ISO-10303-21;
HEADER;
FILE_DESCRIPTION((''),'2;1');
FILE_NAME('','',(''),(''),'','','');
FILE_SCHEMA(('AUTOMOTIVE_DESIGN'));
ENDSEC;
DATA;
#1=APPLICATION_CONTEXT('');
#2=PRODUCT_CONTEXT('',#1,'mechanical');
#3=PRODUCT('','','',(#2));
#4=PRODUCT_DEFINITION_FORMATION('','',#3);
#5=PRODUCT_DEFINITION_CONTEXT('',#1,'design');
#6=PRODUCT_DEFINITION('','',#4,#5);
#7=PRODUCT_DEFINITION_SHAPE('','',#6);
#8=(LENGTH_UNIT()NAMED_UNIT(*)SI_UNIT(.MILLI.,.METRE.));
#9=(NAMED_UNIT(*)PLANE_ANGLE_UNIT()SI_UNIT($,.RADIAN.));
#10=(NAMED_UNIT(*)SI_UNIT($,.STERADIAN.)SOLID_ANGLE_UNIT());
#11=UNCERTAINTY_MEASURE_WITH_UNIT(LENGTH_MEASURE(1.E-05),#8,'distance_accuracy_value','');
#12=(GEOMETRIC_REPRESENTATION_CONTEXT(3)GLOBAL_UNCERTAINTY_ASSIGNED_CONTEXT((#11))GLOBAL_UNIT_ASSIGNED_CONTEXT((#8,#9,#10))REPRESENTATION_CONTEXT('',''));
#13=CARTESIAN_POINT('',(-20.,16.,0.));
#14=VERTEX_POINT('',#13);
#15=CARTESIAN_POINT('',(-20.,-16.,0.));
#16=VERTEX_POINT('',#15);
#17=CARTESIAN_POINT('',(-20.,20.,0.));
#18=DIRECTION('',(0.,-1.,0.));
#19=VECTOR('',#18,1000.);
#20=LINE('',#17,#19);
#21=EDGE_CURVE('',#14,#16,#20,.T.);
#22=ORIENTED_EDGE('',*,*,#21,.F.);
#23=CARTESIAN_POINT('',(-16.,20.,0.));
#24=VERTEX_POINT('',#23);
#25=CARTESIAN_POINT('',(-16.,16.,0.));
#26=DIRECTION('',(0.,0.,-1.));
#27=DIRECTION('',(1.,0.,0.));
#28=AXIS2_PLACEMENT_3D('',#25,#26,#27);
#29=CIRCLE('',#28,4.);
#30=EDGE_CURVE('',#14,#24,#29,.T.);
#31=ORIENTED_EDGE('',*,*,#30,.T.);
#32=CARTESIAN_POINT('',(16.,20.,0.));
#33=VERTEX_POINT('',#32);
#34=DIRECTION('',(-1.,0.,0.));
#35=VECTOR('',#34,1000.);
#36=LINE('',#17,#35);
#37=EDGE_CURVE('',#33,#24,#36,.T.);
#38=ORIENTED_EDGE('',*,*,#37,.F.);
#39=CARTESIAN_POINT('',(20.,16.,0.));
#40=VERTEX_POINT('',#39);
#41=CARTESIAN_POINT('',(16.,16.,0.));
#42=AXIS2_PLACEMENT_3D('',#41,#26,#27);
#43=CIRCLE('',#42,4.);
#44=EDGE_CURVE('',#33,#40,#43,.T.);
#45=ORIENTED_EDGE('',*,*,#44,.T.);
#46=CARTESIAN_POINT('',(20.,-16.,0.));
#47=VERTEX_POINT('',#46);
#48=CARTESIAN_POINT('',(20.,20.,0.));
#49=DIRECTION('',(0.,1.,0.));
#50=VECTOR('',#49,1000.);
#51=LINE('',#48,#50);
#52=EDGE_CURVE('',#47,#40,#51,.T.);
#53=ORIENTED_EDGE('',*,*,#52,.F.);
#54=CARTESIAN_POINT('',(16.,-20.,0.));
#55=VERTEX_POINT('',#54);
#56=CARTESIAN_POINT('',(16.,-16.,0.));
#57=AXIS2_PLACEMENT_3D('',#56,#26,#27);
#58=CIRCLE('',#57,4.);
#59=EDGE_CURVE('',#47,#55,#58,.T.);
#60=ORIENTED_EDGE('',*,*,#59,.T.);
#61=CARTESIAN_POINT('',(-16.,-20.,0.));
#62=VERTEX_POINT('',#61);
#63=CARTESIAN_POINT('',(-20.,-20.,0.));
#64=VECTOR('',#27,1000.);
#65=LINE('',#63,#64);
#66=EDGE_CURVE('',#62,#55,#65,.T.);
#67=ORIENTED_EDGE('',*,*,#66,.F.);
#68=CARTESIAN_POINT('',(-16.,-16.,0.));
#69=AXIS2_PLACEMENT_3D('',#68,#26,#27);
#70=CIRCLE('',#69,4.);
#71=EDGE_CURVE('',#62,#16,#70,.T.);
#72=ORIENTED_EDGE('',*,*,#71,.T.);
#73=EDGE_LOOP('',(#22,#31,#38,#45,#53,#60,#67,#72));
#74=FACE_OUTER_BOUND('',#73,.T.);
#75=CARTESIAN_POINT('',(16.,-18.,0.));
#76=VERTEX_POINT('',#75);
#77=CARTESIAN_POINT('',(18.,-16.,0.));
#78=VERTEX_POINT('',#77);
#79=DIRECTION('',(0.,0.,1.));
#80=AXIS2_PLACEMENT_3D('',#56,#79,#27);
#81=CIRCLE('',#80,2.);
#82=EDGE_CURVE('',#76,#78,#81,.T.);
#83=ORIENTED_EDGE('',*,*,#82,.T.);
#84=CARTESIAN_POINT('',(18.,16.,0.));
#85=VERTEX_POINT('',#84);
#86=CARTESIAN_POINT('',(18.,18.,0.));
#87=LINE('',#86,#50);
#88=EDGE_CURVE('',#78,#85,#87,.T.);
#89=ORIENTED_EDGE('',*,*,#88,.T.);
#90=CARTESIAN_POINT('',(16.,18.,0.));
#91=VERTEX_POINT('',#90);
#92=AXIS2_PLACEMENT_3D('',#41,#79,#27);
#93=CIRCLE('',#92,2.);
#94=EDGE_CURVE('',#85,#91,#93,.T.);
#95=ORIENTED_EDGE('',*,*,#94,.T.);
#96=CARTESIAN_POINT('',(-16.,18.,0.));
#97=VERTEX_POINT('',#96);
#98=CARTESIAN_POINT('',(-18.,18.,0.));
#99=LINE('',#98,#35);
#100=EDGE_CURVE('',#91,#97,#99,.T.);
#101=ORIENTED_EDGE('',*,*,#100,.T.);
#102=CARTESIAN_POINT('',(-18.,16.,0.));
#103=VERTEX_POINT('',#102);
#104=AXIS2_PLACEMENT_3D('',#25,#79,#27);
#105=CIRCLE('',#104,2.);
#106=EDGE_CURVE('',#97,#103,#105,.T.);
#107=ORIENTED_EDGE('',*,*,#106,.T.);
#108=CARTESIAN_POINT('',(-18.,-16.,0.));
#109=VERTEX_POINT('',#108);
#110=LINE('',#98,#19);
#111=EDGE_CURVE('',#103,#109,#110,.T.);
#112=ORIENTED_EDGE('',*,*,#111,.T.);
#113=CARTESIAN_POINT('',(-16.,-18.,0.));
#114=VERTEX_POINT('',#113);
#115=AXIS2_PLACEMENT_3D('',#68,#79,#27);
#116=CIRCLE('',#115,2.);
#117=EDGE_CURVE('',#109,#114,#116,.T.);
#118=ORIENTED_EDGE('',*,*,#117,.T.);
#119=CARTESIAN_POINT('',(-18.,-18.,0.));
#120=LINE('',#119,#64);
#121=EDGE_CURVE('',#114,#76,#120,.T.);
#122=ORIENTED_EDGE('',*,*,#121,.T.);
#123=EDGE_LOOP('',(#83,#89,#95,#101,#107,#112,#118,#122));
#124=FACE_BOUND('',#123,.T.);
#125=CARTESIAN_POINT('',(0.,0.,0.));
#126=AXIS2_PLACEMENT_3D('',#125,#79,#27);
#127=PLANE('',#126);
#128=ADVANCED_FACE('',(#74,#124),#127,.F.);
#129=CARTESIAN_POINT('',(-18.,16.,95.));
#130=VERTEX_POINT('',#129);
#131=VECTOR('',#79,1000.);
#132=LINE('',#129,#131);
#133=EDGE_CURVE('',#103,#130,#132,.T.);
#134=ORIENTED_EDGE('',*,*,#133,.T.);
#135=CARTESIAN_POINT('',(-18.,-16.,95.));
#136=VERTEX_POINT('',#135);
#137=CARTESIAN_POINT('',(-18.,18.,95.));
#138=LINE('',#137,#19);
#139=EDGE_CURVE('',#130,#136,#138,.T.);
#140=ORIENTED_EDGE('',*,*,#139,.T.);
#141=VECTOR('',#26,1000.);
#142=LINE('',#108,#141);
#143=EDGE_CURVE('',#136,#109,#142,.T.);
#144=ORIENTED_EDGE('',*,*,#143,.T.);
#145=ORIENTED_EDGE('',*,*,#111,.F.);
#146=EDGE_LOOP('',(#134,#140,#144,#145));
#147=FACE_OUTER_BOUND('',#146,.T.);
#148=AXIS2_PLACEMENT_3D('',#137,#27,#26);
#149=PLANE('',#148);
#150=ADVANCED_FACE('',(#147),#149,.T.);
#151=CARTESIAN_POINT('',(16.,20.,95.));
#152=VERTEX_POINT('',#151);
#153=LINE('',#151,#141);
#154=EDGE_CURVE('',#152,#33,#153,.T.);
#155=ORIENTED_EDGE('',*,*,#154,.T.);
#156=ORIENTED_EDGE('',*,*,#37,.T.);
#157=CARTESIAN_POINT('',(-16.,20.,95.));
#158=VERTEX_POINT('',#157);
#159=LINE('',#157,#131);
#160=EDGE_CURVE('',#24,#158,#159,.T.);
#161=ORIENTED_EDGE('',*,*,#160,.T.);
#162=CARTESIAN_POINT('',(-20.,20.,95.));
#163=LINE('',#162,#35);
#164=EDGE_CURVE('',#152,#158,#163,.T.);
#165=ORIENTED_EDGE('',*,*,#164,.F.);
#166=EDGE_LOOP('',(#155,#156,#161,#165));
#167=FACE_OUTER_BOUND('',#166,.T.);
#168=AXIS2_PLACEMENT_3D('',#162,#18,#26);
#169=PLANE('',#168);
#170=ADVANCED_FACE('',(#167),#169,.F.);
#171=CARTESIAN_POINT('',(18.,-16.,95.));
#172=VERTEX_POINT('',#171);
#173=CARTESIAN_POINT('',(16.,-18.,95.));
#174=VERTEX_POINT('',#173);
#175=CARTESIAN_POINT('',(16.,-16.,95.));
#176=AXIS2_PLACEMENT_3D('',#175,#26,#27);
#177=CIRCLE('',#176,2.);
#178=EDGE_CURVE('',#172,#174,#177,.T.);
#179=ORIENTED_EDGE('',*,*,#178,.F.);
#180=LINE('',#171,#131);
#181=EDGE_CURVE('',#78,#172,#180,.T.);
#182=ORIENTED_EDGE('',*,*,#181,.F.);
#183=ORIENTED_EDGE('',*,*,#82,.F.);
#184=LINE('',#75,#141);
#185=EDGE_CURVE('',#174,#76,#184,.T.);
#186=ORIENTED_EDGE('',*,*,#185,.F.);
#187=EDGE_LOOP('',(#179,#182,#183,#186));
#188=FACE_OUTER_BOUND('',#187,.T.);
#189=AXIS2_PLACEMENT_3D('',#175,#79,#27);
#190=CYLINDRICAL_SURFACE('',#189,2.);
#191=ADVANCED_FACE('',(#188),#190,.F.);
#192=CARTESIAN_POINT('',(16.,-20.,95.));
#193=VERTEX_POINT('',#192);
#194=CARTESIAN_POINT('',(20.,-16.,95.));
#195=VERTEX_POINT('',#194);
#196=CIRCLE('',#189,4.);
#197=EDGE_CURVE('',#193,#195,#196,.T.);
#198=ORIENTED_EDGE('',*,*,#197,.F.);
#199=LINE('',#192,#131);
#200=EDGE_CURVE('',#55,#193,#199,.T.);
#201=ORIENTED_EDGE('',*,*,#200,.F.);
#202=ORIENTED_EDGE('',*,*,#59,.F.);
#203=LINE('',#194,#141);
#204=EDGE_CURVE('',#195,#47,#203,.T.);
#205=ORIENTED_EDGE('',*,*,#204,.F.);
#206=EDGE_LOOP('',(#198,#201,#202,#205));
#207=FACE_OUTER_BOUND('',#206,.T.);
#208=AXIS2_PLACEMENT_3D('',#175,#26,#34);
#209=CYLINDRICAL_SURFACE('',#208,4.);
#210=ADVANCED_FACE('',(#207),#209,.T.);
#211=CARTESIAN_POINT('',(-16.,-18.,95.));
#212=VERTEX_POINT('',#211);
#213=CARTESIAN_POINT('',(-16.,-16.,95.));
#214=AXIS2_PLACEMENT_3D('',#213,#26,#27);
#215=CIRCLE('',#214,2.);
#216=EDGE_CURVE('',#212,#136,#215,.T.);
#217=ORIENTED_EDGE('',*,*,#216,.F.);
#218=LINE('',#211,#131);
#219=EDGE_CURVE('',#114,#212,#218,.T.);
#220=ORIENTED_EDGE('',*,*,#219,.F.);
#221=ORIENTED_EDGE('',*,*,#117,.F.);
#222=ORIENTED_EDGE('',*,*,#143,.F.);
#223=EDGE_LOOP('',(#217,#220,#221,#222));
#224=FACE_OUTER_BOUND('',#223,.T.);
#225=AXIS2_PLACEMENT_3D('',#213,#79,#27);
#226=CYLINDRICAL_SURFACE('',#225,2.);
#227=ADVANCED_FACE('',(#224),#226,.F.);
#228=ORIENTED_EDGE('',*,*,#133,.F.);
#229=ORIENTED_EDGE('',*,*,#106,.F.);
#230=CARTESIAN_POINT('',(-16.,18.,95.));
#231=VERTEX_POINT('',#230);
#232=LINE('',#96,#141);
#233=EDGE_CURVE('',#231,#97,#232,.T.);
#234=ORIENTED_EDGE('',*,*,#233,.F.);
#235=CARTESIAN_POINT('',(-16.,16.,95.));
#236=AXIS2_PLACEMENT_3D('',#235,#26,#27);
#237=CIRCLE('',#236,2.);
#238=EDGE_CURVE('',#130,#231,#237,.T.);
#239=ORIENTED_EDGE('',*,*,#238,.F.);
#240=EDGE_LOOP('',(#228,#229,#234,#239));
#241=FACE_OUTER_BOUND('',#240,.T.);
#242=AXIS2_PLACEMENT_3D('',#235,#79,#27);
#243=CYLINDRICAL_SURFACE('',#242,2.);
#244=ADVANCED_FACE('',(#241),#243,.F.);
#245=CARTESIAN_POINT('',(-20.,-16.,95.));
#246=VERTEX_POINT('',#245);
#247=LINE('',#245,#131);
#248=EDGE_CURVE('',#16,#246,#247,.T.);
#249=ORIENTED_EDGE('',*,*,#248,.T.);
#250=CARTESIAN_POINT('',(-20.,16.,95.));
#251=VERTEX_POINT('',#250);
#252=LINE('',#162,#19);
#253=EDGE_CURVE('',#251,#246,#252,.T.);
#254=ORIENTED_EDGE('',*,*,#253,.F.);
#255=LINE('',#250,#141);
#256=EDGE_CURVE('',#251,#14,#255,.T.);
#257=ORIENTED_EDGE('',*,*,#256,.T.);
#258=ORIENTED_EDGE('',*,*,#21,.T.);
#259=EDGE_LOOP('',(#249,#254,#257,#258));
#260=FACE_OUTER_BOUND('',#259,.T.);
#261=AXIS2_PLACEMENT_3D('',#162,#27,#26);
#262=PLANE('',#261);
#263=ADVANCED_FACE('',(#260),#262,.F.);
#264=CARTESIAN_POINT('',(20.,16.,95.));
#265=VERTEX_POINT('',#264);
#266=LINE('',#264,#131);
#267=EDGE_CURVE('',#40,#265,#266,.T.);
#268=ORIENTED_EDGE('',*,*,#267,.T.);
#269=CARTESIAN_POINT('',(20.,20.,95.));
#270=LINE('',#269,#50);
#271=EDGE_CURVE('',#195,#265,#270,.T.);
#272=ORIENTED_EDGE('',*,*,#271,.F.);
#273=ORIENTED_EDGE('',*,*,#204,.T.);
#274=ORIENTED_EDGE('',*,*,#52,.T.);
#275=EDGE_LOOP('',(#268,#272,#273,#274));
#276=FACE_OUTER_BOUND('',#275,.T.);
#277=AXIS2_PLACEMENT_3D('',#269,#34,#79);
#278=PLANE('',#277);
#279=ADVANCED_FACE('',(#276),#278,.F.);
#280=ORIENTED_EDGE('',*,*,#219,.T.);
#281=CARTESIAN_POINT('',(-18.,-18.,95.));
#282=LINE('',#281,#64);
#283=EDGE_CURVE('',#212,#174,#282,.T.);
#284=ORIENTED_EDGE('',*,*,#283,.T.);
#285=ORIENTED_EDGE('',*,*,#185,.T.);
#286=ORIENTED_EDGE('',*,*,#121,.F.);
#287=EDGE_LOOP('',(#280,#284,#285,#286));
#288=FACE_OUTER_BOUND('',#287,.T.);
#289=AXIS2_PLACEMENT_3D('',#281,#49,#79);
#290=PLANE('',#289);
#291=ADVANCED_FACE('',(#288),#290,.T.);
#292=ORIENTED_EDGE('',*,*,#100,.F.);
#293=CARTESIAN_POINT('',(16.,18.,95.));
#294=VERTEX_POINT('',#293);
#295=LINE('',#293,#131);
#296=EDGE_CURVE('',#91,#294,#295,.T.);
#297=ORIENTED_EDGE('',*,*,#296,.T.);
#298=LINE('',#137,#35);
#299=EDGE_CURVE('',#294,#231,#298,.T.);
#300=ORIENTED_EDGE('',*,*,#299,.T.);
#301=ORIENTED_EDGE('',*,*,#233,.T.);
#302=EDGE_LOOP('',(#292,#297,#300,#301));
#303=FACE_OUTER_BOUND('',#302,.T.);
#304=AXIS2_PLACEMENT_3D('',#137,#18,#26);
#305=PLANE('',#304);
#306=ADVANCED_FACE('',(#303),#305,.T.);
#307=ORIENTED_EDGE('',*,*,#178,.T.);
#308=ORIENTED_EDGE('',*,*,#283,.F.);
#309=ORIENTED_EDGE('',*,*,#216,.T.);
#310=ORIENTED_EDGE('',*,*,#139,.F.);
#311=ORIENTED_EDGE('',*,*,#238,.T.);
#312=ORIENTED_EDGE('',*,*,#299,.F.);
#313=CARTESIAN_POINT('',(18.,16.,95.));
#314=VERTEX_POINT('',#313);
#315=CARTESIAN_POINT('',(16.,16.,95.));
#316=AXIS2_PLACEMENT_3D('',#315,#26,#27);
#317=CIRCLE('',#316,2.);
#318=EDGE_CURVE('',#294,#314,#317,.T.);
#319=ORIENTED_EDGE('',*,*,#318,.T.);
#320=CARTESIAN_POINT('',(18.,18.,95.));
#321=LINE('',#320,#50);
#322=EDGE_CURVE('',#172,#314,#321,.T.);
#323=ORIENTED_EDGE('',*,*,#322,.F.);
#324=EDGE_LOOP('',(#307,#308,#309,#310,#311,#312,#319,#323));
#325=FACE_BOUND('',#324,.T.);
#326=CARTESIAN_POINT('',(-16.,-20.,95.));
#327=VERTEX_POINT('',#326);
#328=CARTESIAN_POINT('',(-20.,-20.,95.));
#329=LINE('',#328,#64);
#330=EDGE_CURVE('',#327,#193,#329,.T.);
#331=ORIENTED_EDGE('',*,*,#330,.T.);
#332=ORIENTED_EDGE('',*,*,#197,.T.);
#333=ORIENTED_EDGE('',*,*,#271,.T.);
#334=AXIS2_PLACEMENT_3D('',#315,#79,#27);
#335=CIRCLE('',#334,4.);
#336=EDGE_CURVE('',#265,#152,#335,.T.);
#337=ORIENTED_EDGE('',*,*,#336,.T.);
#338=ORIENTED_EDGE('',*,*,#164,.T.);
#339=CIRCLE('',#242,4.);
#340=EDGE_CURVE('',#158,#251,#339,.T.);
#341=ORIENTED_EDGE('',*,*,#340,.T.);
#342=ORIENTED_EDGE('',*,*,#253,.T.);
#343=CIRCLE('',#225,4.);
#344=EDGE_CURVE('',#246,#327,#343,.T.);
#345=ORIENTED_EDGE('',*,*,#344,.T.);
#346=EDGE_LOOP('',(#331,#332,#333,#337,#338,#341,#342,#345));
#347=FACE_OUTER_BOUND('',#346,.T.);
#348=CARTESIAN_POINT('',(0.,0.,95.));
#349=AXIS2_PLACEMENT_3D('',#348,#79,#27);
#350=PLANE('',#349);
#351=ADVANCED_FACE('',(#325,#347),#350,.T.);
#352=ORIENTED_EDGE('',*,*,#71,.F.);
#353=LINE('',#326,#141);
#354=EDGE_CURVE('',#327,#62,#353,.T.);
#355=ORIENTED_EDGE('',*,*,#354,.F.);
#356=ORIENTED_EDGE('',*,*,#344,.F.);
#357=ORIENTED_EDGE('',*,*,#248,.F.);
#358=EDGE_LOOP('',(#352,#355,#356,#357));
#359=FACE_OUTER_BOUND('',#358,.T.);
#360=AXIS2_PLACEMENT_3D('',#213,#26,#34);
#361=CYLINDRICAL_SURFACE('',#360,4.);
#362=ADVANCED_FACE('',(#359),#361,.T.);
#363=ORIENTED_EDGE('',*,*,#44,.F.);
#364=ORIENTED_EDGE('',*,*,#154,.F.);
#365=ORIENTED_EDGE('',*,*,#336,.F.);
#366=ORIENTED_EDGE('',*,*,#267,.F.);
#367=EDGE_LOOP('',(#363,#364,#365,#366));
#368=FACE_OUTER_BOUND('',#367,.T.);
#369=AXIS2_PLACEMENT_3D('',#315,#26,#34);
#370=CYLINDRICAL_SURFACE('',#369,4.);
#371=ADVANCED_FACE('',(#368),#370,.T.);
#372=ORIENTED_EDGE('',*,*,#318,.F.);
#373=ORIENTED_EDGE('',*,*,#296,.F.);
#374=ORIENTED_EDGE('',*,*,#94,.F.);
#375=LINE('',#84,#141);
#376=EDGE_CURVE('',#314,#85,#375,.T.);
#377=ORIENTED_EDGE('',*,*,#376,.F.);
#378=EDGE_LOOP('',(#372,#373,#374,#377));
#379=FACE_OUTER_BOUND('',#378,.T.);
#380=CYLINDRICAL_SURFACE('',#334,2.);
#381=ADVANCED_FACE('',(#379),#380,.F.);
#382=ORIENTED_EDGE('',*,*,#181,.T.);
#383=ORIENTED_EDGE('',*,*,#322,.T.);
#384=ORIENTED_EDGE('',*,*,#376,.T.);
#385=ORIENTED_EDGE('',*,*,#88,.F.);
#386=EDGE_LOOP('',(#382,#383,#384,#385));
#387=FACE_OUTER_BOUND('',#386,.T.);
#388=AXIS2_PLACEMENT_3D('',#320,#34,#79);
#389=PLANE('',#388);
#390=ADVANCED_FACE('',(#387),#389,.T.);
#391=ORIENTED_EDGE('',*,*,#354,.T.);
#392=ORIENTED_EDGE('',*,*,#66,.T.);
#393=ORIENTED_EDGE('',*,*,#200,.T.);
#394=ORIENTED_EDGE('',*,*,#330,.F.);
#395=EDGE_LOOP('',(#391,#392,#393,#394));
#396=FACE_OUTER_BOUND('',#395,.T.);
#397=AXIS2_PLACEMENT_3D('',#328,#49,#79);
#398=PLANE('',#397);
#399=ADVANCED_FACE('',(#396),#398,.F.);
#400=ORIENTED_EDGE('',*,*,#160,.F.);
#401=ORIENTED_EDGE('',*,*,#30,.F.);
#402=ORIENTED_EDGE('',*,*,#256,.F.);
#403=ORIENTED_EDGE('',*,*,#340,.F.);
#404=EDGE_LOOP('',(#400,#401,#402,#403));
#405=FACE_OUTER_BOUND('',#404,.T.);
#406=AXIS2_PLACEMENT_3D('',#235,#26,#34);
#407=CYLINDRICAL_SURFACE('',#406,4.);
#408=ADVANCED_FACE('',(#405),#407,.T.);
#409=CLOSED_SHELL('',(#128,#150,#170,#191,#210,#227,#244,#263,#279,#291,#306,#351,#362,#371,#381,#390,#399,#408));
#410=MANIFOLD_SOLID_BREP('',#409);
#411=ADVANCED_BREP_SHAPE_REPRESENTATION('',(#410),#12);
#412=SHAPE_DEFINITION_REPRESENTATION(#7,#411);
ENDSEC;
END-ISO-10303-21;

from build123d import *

# Parameters (mm, degrees)
SKETCH1_W           = 40
SKETCH1_H           = 40
SKETCH1_W_2         = 36
SKETCH1_H_2         = 36
BOSS_EXTRUDE1_DEPTH = 95
FILLET1_R           = 2
FILLET2_R           = 4


with BuildPart() as part:
    # Sketch1 → Boss-Extrude1 (new body)
    with BuildSketch(Plane.XY):
        Rectangle(SKETCH1_W, SKETCH1_H)
        Rectangle(SKETCH1_W_2, SKETCH1_H_2, mode=Mode.SUBTRACT)
    extrude(amount=BOSS_EXTRUDE1_DEPTH)

    # Fillet1
    fillet1_edges = [part.edges().sort_by_distance(p)[0] for p in [
        (18, -18, 47.5),
        (18, 18, 47.5),
        (-18, 18, 47.5),
        (-18, -18, 47.5),
    ]]
    fillet(fillet1_edges, radius=FILLET1_R)

    # Fillet2
    fillet2_edges = [part.edges().sort_by_distance(p)[0] for p in [
        (20, -20, 47.5),
        (-20, -20, 47.5),
        (-20, 20, 47.5),
        (20, 20, 47.5),
    ]]
    fillet(fillet2_edges, radius=FILLET2_R)


solid = part.part
